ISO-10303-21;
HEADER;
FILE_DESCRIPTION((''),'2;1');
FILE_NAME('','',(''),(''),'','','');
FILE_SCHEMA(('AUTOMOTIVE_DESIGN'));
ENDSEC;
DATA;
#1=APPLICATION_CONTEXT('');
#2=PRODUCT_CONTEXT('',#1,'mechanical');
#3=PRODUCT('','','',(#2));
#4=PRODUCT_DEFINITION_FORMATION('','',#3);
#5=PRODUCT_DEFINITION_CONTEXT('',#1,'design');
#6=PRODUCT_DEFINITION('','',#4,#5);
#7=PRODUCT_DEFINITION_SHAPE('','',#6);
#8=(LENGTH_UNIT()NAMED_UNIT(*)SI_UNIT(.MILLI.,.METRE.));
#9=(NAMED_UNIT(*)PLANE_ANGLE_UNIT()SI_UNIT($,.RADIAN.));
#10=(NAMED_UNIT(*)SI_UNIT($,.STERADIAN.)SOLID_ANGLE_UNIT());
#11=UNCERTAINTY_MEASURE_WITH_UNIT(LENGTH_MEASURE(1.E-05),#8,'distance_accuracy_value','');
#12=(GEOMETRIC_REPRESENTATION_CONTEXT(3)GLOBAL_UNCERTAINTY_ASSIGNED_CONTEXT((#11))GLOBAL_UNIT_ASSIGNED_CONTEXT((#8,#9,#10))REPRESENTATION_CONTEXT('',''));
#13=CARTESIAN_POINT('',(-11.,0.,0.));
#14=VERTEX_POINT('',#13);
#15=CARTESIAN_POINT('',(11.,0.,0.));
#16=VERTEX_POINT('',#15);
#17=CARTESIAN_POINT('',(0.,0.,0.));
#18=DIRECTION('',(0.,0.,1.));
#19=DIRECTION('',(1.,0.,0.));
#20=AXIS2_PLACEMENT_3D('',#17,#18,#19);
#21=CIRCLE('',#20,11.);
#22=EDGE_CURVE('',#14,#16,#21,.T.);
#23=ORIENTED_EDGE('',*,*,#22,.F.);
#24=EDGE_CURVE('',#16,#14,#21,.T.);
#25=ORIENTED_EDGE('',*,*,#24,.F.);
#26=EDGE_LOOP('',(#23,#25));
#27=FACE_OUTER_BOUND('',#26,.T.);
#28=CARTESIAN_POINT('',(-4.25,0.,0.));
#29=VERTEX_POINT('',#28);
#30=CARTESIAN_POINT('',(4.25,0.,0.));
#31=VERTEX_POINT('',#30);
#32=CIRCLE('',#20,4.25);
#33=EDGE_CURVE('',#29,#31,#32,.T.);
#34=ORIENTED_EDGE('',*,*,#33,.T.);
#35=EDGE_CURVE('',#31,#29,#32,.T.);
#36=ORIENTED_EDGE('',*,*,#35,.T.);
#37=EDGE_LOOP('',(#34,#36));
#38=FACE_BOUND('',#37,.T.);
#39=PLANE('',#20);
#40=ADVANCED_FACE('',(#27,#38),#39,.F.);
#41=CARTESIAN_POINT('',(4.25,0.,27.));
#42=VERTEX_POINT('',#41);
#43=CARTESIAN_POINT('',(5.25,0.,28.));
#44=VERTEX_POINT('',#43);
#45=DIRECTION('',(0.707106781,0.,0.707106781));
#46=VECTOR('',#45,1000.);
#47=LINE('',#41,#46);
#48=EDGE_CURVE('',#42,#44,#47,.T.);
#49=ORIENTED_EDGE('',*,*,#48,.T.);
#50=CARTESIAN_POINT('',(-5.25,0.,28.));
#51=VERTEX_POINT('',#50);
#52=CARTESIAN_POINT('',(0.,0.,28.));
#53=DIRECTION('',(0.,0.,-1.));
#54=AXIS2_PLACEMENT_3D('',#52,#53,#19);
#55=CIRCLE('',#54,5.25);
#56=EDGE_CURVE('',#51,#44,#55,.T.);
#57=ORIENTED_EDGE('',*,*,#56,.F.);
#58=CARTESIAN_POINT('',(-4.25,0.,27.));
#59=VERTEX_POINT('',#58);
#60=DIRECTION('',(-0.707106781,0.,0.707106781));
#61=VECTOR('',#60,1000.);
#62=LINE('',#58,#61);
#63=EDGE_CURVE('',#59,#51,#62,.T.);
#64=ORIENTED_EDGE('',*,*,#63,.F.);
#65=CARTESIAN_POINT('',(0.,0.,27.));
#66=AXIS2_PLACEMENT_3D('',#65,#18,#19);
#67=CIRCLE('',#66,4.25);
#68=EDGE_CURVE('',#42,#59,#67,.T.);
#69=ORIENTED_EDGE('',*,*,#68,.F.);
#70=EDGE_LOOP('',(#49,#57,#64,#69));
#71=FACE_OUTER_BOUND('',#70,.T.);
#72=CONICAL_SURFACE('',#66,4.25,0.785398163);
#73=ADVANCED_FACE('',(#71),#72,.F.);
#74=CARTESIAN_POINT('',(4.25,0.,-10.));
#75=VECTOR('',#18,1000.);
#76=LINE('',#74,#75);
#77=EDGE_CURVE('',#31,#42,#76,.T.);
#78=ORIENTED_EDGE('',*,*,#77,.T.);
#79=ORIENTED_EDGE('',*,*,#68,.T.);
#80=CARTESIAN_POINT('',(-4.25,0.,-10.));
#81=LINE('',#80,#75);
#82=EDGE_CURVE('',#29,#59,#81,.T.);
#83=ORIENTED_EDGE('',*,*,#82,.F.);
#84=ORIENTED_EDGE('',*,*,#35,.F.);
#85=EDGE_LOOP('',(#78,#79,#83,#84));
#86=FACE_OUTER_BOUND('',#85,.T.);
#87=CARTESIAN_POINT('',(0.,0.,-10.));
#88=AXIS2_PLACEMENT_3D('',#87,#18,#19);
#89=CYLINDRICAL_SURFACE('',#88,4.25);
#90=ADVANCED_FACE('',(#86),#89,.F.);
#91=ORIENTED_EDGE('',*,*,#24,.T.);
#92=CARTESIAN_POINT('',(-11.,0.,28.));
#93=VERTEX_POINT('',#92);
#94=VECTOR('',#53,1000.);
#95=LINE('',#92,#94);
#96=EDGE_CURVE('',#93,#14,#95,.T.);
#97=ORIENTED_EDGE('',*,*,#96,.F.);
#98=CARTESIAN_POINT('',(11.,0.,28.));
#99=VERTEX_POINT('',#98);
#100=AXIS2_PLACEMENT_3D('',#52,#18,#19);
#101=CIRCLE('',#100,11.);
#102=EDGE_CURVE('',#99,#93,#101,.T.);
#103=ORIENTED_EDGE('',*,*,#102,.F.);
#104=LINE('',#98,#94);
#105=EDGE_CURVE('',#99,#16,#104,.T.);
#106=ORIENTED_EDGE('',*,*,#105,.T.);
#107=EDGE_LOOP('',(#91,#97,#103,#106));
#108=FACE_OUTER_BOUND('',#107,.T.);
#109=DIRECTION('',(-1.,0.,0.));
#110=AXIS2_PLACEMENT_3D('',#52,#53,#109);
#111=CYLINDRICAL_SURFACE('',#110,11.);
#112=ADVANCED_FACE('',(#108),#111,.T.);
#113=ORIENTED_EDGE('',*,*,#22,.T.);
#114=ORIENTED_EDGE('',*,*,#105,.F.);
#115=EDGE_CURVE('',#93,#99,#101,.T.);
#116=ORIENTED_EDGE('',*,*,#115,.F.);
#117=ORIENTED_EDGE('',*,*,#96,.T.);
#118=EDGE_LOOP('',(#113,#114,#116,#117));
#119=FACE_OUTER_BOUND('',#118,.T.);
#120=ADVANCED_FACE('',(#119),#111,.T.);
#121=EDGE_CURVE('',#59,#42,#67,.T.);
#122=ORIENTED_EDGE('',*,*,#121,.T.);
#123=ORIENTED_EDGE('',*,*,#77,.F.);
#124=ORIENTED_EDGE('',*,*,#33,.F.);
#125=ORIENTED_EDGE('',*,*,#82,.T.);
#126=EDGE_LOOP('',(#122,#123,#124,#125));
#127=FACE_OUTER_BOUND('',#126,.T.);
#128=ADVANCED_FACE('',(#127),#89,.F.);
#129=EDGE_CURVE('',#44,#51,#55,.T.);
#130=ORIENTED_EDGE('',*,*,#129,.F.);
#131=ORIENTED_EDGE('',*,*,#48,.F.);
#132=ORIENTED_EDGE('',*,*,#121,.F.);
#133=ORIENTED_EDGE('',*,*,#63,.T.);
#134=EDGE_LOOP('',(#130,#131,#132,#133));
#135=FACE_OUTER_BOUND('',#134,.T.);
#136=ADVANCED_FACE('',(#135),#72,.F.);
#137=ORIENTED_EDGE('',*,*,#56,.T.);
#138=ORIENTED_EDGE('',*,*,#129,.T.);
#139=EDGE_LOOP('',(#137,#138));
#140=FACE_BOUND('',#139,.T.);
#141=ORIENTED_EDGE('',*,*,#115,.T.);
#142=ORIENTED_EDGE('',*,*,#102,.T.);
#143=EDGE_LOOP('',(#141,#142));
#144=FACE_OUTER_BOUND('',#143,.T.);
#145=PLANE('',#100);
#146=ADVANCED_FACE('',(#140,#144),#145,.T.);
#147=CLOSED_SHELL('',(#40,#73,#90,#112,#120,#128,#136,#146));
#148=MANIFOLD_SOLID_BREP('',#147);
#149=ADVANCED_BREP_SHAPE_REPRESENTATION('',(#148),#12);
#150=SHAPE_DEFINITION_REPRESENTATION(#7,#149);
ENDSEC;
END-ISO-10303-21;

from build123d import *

# Parameters (mm, degrees)
SKETCH1_R           = 11
BOSS_EXTRUDE1_DEPTH = 28
SKETCH2_R           = 4.25
CUT_EXTRUDE1_DEPTH  = 38
CHAMFER1_SIZE       = 1


with BuildPart() as part:
    # Sketch1 → Boss-Extrude1 (new body)
    with BuildSketch(Plane.XY):
        Circle(SKETCH1_R)
    extrude(amount=BOSS_EXTRUDE1_DEPTH)

    # Sketch2 → Cut-Extrude1 (cut)
    with BuildSketch(Plane.XY.offset(28)):
        Circle(SKETCH2_R)
    extrude(amount=-CUT_EXTRUDE1_DEPTH, mode=Mode.SUBTRACT)

    # Chamfer1
    chamfer1_edges = [part.edges().sort_by_distance(p)[0] for p in [
        (-4.25, 0, 28),
    ]]
    chamfer(chamfer1_edges, length=CHAMFER1_SIZE)


solid = part.part
